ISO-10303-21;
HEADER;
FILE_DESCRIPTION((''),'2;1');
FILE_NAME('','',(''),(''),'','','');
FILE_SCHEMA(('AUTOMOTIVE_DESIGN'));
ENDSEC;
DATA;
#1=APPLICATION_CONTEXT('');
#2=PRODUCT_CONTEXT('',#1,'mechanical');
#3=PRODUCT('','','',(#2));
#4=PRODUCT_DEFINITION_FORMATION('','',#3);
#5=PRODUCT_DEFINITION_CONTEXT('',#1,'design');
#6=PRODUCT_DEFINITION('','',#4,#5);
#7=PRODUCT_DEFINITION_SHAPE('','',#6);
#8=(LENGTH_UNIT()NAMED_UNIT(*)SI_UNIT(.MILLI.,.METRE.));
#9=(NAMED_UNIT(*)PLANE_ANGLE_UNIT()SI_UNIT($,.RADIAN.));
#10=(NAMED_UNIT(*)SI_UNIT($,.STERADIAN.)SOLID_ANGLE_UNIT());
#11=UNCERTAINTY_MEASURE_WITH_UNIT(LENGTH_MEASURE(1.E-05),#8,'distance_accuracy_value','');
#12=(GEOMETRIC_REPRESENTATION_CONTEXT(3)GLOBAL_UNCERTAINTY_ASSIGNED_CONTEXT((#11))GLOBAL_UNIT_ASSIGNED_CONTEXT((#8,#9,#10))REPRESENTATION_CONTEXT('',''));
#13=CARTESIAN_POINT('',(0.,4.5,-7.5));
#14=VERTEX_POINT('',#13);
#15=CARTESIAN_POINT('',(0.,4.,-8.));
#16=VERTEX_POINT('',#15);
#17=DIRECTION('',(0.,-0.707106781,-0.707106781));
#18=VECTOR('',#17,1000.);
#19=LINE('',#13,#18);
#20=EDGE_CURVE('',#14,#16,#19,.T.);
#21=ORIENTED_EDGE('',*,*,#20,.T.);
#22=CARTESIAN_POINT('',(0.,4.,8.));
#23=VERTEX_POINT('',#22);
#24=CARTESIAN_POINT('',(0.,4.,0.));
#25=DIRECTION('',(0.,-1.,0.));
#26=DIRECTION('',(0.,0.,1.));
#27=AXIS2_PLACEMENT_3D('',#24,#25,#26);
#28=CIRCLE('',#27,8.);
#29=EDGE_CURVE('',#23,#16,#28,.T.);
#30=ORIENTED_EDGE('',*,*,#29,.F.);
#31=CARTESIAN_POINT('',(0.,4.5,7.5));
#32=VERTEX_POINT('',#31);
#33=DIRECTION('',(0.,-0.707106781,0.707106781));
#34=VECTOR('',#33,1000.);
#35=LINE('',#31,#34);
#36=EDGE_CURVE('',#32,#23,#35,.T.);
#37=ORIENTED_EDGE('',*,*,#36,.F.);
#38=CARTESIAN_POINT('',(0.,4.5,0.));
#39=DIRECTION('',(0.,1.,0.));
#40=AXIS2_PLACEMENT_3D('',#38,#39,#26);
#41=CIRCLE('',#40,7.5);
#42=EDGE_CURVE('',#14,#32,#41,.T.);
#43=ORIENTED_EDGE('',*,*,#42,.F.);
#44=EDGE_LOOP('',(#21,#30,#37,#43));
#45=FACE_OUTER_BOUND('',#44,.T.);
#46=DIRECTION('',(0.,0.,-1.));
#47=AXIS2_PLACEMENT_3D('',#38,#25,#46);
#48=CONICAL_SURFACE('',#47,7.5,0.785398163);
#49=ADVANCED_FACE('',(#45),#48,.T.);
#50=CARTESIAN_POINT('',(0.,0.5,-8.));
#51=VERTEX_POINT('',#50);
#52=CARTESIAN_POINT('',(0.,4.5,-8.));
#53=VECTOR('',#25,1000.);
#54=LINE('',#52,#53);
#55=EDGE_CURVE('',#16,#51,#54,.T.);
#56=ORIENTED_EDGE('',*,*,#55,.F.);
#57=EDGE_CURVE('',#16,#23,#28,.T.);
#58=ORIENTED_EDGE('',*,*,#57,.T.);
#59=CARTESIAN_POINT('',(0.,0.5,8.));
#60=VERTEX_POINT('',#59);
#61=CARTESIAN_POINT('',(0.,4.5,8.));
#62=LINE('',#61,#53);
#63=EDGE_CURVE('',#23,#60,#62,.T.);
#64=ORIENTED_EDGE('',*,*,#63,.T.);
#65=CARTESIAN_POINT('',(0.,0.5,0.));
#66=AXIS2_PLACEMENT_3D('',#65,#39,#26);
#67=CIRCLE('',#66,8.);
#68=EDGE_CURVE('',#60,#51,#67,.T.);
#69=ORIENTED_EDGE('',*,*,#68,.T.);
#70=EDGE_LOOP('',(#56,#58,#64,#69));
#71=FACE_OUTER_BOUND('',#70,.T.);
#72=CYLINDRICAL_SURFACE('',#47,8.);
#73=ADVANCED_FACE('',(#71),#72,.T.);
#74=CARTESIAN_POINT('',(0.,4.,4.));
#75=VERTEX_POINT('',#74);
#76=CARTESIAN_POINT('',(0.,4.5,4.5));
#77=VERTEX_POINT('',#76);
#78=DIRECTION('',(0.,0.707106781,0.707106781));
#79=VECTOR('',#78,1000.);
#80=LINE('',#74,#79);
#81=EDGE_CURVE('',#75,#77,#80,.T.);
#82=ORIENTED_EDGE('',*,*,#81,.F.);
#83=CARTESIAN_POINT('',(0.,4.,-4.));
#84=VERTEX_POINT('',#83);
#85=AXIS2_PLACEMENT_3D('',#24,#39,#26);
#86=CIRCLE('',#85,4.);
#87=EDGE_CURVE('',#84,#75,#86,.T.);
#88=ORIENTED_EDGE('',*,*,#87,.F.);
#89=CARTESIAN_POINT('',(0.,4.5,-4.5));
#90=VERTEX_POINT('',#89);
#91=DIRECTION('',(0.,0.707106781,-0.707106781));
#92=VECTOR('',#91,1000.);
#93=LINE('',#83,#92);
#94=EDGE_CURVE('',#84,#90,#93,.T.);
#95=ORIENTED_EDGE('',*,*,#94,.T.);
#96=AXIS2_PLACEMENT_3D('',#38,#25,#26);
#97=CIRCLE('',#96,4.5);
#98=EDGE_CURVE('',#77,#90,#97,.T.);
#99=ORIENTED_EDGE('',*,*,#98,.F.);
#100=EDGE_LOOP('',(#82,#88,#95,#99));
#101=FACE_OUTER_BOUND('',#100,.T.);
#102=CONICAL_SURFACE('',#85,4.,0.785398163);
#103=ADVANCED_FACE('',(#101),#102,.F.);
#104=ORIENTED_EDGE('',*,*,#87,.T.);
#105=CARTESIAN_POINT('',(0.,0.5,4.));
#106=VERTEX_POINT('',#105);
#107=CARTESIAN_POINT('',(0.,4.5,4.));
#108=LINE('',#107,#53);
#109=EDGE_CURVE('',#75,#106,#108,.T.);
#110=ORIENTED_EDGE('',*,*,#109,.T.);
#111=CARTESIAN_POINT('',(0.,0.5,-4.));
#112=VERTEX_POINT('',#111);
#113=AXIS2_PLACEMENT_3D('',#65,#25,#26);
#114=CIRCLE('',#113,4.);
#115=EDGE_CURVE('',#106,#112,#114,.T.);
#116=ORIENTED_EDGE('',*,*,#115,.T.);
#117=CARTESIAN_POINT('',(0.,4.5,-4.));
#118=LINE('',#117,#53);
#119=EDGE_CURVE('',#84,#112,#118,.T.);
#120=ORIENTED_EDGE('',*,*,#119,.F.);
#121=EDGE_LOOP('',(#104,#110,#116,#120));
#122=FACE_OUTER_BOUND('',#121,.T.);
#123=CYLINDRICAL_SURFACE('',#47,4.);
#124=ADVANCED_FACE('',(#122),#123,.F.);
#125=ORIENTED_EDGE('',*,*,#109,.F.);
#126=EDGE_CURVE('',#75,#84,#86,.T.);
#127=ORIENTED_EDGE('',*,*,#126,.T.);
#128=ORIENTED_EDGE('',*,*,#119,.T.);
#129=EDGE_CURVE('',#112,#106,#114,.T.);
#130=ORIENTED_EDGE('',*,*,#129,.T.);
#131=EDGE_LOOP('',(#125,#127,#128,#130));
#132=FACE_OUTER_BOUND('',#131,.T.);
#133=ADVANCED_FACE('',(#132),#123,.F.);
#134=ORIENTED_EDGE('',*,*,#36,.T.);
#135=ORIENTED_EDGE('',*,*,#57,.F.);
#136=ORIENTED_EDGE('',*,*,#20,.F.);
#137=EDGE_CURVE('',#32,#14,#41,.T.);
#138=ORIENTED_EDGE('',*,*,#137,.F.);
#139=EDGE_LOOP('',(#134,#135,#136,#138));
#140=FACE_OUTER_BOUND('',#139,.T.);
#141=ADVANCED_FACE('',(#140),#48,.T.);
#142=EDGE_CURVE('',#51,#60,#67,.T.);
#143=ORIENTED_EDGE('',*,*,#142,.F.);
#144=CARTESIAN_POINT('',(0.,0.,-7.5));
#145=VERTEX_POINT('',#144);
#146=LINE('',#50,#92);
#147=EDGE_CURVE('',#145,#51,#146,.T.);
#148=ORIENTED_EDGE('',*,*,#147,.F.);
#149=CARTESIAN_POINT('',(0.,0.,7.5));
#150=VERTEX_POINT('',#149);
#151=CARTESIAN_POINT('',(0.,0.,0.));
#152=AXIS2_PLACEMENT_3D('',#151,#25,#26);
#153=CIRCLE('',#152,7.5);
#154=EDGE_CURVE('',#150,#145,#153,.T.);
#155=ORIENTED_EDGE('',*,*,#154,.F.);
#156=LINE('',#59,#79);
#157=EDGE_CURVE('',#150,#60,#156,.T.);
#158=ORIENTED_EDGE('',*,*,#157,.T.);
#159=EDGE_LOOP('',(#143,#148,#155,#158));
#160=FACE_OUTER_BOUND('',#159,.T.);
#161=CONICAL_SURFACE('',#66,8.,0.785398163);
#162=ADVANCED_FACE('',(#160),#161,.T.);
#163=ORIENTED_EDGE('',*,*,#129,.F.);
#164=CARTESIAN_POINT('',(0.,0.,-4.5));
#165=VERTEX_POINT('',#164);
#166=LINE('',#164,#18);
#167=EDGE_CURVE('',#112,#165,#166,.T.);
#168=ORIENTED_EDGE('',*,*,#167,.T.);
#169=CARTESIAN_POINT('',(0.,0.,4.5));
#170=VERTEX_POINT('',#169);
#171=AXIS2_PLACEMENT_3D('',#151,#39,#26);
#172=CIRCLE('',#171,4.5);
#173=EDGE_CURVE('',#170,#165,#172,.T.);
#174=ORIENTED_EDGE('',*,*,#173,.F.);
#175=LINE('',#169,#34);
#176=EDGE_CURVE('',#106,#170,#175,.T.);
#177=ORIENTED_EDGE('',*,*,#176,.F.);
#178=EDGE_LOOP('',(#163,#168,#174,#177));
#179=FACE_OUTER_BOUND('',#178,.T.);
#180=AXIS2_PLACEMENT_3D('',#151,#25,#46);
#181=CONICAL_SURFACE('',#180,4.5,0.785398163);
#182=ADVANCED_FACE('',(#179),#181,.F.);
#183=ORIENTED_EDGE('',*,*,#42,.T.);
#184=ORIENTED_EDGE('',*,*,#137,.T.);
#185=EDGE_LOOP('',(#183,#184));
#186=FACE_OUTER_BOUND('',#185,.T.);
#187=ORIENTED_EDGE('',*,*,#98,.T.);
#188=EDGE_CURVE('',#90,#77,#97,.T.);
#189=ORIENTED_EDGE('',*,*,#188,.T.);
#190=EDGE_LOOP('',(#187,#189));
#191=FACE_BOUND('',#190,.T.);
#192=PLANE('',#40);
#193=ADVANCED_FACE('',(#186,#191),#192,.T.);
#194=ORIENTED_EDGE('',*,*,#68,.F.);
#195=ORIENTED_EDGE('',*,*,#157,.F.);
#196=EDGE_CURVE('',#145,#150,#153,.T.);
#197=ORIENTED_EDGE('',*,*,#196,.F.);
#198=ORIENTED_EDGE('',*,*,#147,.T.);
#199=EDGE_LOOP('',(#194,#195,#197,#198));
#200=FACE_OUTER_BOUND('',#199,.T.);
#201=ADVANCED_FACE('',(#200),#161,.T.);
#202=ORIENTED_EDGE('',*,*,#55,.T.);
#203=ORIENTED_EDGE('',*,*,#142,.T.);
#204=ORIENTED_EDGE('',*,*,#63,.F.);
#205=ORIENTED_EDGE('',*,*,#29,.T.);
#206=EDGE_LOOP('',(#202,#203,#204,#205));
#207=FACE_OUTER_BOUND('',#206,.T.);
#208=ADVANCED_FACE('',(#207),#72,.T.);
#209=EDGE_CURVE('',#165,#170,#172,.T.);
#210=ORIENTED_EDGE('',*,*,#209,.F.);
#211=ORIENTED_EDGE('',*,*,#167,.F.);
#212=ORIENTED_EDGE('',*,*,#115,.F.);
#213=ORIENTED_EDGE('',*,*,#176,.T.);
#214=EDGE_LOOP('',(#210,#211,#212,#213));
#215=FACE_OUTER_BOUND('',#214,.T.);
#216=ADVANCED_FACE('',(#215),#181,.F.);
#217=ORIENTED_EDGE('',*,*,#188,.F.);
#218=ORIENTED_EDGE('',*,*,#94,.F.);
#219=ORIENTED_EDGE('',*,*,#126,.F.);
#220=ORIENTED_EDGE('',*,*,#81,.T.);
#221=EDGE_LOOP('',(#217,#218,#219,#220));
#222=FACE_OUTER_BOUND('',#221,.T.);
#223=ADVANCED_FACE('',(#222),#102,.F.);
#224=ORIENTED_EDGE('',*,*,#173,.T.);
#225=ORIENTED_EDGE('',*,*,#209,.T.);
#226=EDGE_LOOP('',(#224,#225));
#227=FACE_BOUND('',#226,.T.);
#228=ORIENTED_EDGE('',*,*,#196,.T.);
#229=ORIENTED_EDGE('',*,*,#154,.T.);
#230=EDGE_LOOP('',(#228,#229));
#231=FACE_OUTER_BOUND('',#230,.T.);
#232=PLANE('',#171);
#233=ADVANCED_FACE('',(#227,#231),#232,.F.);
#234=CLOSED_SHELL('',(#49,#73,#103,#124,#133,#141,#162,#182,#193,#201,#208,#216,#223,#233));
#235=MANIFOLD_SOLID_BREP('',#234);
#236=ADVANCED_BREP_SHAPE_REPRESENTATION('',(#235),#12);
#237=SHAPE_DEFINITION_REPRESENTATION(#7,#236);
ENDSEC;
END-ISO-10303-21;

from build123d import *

# Parameters (mm, degrees)
SKETCH1_R           = 8
SKETCH1_R_2         = 4
BOSS_EXTRUDE1_DEPTH = 4.5
CHAMFER1_SIZE       = 0.5


with BuildPart() as part:
    # Sketch1 → Boss-Extrude1 (new body)
    with BuildSketch(Plane(origin=(0, 0, 0), x_dir=(1, 0, 0), z_dir=(0, 1, 0))):
        with Locations(Location((0, 0, 0), (0, 0, 270))):
            Circle(SKETCH1_R)
        with Locations(Location((0, 0, 0), (0, 0, 270))):
            Circle(SKETCH1_R_2, mode=Mode.SUBTRACT)
    extrude(amount=BOSS_EXTRUDE1_DEPTH)

    # Chamfer1
    chamfer1_edges = [part.edges().sort_by_distance(p)[0] for p in [
        (0, 0, -8),
        (0, 4.5, -8),
        (0, 0, -4),
        (0, 4.5, -4),
    ]]
    chamfer(chamfer1_edges, length=CHAMFER1_SIZE)


solid = part.part
